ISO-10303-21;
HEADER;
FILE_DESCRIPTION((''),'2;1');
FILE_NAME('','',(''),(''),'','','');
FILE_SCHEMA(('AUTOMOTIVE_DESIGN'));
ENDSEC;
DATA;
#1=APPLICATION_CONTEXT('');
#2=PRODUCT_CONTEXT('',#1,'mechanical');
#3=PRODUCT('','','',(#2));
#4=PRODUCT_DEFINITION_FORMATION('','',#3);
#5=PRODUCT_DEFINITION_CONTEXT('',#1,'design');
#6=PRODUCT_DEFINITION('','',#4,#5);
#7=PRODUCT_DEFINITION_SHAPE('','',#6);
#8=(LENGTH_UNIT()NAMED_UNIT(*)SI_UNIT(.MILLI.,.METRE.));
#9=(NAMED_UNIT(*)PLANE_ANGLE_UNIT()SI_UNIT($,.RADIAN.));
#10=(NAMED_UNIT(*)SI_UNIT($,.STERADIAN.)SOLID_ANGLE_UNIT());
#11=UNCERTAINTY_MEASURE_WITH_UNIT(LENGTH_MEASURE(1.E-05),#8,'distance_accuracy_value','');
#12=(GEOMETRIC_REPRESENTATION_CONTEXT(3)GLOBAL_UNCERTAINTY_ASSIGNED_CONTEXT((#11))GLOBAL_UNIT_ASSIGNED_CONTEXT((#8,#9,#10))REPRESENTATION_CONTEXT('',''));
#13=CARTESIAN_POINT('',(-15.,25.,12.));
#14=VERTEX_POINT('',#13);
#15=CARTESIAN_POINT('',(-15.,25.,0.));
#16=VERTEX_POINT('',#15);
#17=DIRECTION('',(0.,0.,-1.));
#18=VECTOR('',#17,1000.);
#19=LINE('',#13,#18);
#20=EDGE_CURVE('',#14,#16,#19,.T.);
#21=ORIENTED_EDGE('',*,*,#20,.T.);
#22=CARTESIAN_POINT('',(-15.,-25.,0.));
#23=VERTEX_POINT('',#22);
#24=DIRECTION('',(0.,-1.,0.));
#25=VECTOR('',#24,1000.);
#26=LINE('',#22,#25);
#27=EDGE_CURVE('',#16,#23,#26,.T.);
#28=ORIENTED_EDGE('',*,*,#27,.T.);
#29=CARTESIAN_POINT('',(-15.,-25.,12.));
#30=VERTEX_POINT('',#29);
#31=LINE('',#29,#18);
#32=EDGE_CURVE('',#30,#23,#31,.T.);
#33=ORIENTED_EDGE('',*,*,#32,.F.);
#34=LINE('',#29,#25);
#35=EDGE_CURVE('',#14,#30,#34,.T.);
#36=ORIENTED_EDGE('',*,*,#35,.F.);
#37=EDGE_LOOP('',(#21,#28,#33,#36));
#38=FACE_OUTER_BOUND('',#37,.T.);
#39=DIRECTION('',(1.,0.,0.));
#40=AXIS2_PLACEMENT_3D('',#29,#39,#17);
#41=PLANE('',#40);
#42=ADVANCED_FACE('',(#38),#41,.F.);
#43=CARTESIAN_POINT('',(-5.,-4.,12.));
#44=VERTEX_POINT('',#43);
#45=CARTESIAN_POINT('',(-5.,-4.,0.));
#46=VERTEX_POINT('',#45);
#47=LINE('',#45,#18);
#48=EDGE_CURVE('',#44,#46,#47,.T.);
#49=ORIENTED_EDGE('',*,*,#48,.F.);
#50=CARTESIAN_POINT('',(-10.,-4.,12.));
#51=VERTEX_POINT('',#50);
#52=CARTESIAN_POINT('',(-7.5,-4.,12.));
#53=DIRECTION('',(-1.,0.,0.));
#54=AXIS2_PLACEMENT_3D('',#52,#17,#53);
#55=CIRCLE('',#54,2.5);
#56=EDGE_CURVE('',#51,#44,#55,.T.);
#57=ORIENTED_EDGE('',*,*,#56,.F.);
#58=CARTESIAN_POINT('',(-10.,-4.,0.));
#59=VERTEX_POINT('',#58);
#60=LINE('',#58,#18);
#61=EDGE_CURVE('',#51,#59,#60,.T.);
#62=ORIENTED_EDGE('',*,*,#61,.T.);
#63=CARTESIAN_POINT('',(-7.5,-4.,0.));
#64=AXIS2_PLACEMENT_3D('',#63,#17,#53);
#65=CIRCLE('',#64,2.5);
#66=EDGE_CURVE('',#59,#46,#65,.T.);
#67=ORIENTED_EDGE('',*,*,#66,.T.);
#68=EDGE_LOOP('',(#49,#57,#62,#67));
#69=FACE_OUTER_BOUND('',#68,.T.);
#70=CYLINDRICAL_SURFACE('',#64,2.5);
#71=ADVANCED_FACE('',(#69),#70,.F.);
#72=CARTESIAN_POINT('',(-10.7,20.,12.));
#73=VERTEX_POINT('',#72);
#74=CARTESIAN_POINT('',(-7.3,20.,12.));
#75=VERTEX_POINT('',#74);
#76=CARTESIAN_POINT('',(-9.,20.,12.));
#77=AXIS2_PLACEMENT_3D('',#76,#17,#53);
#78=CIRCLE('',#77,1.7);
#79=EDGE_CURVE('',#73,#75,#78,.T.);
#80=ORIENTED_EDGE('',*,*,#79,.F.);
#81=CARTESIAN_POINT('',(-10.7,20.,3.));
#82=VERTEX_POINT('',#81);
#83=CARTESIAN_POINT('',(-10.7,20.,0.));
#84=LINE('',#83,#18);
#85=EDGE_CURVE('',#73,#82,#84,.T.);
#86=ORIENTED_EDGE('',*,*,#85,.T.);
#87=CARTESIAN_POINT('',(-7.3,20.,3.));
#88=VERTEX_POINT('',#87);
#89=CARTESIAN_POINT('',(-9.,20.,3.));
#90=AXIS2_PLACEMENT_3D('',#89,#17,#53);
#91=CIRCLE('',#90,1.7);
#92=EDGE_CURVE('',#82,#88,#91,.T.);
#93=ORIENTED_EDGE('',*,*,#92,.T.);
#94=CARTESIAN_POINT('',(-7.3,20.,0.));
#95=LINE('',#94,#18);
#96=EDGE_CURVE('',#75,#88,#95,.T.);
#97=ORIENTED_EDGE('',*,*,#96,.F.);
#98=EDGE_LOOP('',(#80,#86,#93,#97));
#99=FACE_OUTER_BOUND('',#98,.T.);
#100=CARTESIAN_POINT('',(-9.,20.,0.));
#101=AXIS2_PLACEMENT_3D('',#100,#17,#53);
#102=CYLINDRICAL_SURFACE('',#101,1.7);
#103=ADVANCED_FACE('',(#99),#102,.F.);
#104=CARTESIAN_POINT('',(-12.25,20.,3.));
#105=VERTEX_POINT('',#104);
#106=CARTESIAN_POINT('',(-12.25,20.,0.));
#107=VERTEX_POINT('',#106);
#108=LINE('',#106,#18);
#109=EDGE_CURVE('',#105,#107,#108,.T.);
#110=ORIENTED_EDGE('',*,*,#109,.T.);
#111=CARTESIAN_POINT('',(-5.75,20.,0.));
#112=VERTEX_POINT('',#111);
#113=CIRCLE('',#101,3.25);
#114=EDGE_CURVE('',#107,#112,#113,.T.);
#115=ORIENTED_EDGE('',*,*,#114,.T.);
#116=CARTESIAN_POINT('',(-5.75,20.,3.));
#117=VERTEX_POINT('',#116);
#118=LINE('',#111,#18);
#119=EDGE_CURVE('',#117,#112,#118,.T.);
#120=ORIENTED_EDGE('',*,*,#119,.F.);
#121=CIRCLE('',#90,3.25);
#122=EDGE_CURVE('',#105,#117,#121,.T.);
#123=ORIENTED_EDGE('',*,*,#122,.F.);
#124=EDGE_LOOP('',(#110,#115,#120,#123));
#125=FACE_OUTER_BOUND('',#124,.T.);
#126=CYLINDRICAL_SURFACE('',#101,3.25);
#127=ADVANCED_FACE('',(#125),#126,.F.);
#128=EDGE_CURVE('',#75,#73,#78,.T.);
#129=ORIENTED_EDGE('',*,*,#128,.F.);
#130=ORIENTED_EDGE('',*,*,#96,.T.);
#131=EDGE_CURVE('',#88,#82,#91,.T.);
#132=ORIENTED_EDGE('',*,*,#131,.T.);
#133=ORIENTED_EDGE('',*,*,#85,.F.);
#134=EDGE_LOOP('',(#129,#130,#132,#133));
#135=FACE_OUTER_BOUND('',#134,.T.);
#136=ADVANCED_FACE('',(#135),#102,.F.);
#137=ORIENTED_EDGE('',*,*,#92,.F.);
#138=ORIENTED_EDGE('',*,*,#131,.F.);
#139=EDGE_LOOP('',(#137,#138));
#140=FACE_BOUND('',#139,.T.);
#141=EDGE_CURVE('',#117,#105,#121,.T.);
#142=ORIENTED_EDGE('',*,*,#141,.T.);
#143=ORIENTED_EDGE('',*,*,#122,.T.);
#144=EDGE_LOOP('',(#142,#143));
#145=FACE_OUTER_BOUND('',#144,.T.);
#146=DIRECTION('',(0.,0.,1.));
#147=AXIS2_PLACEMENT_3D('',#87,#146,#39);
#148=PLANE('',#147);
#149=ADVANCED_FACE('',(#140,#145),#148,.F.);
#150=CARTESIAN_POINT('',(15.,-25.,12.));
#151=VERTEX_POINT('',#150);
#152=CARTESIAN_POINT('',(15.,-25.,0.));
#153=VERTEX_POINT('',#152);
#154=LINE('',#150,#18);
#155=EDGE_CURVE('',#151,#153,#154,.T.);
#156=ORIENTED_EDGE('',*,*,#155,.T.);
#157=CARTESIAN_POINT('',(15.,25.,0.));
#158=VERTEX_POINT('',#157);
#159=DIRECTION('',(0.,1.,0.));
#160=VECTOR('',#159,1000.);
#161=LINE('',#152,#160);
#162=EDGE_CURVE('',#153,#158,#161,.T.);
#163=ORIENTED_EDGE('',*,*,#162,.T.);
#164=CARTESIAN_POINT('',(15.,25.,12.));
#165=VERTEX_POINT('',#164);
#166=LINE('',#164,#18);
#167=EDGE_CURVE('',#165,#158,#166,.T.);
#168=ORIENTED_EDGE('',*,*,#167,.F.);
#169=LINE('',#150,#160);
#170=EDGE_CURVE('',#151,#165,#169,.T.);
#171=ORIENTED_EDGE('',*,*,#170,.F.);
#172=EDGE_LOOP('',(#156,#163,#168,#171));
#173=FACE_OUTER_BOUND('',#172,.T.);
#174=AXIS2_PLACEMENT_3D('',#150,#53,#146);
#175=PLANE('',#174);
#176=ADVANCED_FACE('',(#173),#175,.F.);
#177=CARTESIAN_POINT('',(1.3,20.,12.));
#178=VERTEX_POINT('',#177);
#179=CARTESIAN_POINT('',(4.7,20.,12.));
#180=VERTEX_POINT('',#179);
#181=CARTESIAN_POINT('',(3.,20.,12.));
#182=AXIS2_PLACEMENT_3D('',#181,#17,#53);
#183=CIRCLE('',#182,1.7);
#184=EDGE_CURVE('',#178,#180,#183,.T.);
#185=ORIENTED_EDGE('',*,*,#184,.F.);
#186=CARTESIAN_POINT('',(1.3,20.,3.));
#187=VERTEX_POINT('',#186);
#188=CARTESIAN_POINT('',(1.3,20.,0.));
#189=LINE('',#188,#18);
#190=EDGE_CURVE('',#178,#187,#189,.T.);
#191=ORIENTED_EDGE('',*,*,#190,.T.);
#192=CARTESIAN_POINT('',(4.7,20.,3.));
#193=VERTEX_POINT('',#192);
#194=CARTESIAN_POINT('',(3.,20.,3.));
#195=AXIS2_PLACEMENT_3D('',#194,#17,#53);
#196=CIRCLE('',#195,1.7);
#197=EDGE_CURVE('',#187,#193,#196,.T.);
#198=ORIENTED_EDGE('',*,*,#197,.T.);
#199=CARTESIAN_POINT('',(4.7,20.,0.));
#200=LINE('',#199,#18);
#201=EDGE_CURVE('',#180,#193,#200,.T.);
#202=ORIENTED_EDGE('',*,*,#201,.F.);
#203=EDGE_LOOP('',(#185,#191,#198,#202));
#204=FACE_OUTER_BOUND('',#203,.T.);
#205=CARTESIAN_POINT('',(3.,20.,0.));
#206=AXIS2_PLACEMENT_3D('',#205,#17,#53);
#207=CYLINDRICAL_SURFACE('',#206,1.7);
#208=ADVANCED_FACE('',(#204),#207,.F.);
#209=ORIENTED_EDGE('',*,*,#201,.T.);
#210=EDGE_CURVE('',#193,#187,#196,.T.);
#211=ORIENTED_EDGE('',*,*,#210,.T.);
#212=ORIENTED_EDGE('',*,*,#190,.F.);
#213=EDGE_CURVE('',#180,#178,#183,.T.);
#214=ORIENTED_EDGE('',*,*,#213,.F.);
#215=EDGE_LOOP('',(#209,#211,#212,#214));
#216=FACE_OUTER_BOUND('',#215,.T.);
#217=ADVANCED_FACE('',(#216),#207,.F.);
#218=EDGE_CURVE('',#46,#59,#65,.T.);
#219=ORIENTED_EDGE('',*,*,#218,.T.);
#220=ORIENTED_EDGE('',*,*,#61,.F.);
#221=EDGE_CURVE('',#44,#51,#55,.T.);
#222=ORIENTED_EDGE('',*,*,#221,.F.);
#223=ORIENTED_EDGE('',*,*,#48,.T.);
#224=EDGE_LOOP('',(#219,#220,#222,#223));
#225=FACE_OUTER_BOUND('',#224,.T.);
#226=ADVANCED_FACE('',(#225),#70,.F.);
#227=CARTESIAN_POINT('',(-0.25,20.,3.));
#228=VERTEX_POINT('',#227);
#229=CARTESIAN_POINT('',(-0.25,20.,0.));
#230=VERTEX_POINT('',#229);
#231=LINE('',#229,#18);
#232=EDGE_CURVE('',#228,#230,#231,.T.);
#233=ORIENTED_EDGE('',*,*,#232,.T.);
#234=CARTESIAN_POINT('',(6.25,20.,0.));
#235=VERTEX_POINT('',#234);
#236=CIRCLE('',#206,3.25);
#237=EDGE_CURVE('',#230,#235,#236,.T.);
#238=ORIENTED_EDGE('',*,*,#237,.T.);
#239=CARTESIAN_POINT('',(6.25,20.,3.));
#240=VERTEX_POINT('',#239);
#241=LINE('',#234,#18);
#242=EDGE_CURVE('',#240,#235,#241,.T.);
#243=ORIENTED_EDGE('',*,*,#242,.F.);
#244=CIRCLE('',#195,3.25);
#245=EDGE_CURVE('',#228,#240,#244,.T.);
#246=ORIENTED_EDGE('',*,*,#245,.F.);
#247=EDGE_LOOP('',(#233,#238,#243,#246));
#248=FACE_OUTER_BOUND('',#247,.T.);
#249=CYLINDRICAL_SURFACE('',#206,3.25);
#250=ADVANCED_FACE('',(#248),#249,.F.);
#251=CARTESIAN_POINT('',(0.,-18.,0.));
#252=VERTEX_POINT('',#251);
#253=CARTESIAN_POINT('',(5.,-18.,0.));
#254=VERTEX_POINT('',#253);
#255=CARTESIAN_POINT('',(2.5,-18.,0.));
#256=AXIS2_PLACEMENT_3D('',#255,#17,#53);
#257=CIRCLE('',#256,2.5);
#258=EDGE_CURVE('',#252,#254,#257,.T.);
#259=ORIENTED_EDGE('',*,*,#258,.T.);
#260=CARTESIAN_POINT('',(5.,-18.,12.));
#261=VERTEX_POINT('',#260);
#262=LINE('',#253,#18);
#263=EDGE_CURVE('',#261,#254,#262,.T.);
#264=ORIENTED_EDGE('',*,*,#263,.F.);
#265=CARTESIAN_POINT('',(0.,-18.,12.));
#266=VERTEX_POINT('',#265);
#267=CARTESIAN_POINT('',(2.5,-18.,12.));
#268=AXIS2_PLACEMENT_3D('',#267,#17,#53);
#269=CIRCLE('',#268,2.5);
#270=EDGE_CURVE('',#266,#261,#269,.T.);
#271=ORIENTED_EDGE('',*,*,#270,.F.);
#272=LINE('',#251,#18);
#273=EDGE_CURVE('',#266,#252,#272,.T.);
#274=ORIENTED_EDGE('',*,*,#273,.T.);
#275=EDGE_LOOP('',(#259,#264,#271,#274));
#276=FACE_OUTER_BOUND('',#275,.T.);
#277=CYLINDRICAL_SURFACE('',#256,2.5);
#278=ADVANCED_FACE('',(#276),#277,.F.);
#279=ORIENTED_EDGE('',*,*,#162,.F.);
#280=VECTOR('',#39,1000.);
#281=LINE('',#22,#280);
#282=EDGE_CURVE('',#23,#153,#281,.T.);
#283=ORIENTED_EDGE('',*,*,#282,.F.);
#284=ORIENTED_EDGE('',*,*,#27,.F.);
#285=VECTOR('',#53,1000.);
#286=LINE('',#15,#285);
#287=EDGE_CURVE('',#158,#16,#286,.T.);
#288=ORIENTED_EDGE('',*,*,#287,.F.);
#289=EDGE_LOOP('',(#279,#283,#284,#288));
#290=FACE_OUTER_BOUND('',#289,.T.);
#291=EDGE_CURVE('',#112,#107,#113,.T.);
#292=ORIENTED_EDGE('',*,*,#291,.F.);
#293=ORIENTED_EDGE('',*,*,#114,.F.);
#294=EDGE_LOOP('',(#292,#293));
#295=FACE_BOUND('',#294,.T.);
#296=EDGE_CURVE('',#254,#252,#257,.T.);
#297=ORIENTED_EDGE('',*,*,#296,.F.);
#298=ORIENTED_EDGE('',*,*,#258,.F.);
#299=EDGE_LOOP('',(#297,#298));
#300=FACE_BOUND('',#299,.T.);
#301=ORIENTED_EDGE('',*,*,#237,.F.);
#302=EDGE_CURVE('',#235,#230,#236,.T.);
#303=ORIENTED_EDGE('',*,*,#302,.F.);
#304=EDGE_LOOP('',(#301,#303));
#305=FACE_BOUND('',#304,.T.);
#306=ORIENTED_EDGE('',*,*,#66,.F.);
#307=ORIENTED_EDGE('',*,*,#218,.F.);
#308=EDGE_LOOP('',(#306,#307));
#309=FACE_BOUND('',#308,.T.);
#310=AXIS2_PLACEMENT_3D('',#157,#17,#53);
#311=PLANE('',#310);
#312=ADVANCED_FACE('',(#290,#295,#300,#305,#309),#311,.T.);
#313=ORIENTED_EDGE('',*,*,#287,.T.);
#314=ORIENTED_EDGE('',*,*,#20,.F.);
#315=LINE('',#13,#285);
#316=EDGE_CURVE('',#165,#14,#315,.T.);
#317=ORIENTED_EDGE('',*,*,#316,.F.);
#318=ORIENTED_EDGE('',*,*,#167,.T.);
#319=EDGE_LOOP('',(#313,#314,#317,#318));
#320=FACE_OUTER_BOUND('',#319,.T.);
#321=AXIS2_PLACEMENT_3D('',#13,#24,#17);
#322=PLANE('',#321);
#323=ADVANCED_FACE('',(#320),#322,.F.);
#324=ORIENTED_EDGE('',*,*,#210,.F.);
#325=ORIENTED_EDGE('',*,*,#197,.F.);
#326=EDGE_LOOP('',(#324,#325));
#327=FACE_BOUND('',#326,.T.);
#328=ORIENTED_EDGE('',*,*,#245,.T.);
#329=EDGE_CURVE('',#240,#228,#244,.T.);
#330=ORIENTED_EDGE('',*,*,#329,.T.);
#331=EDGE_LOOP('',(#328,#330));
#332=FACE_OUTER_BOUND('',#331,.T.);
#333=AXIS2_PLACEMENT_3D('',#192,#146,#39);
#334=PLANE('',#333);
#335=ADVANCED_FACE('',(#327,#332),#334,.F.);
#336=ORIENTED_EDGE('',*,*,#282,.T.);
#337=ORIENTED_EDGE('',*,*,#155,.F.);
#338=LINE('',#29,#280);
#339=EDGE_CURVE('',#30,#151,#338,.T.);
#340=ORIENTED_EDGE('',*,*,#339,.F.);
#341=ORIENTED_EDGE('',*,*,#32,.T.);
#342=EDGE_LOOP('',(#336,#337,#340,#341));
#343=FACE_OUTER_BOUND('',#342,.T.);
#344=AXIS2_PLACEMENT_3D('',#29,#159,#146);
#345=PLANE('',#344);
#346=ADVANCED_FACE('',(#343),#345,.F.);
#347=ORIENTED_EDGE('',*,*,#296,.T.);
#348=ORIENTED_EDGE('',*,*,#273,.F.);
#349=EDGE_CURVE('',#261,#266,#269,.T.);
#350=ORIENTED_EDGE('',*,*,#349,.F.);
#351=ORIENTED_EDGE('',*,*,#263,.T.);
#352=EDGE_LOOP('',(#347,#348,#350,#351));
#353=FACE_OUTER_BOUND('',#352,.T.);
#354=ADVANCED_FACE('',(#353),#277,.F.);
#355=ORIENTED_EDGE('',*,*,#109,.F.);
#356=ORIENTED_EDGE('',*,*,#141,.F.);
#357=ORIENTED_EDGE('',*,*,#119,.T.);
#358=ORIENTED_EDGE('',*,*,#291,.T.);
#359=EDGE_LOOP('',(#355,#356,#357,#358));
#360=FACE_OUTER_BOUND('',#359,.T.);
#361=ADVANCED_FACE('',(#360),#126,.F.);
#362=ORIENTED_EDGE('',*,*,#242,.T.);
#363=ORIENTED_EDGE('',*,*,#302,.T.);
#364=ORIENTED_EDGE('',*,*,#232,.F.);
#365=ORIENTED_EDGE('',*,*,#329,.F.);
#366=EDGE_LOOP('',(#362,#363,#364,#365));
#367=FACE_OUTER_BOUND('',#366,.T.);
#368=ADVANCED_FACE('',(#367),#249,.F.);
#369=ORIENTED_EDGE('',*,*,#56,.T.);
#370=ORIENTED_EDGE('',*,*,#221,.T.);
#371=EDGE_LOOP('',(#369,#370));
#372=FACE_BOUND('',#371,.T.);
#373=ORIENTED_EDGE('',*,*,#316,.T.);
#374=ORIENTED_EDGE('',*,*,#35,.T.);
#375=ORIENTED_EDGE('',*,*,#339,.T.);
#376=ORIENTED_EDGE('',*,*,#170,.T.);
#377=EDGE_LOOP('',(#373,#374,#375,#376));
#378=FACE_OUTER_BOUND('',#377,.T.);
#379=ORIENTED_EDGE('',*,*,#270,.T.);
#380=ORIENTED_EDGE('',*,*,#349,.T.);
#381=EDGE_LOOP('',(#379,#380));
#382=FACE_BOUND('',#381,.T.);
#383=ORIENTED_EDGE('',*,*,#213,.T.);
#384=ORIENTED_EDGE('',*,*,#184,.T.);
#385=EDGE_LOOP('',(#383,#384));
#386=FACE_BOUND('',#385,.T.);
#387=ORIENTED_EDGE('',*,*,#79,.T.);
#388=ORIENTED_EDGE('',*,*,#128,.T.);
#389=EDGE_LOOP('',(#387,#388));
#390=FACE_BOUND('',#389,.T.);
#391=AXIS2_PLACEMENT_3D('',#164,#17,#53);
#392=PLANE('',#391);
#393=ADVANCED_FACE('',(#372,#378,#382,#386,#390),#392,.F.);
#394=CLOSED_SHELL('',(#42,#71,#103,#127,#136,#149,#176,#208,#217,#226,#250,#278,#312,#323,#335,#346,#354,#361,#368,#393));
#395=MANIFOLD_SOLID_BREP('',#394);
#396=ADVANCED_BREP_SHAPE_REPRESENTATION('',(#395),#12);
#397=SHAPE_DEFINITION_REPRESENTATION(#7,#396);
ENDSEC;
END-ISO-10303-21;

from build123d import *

# Parameters (mm, degrees)
SKETCH_1_W                                         = 30
SKETCH_1_H                                         = 50
BOSS_EXTRUDE_1_DEPTH                               = 12
M6_TAPPED_HOLE_1_D                                 = 5
M3_SOCKET_HEAD_CAP_SCREW_COUNTERBORE_1_D           = 3.4
M3_SOCKET_HEAD_CAP_SCREW_COUNTERBORE_1_CBORE_D     = 6.5
M3_SOCKET_HEAD_CAP_SCREW_COUNTERBORE_1_CBORE_DEPTH = 3
LINEAR_PATTERN_1_COUNT                             = 2
LINEAR_PATTERN_1_PITCH                             = 12


with BuildPart() as part:
    # Sketch 1 → Boss-Extrude 1 (new body)
    with BuildSketch(Plane.XY):
        Rectangle(SKETCH_1_W, SKETCH_1_H)
    extrude(amount=BOSS_EXTRUDE_1_DEPTH)

    # M6 Tapped Hole 1 (through all)
    with Locations(Plane(origin=(0, 0, 0), x_dir=(-1, 0, 0), z_dir=(0, 0, -1))):
        with Locations((7.5, -4), (-2.5, -18)):
            Hole(M6_TAPPED_HOLE_1_D / 2)

    # M3 Socket Head Cap Screw Counterbore 1 (through all)
    with Locations(Plane(origin=(0, 0, 0), x_dir=(-1, 0, 0), z_dir=(0, 0, -1))):
        with Locations((9, 20)):
            m3_socket_head_cap_screw_counterbore_1 = CounterBoreHole(M3_SOCKET_HEAD_CAP_SCREW_COUNTERBORE_1_D / 2, M3_SOCKET_HEAD_CAP_SCREW_COUNTERBORE_1_CBORE_D / 2, M3_SOCKET_HEAD_CAP_SCREW_COUNTERBORE_1_CBORE_DEPTH)

    # Linear Pattern 1: M3 Socket Head Cap Screw Counterbore 1 ×2
    with Locations(*[(i * LINEAR_PATTERN_1_PITCH, 0, 0) for i in range(1, LINEAR_PATTERN_1_COUNT)]):
        add(m3_socket_head_cap_screw_counterbore_1, mode=Mode.SUBTRACT)


solid = part.part
